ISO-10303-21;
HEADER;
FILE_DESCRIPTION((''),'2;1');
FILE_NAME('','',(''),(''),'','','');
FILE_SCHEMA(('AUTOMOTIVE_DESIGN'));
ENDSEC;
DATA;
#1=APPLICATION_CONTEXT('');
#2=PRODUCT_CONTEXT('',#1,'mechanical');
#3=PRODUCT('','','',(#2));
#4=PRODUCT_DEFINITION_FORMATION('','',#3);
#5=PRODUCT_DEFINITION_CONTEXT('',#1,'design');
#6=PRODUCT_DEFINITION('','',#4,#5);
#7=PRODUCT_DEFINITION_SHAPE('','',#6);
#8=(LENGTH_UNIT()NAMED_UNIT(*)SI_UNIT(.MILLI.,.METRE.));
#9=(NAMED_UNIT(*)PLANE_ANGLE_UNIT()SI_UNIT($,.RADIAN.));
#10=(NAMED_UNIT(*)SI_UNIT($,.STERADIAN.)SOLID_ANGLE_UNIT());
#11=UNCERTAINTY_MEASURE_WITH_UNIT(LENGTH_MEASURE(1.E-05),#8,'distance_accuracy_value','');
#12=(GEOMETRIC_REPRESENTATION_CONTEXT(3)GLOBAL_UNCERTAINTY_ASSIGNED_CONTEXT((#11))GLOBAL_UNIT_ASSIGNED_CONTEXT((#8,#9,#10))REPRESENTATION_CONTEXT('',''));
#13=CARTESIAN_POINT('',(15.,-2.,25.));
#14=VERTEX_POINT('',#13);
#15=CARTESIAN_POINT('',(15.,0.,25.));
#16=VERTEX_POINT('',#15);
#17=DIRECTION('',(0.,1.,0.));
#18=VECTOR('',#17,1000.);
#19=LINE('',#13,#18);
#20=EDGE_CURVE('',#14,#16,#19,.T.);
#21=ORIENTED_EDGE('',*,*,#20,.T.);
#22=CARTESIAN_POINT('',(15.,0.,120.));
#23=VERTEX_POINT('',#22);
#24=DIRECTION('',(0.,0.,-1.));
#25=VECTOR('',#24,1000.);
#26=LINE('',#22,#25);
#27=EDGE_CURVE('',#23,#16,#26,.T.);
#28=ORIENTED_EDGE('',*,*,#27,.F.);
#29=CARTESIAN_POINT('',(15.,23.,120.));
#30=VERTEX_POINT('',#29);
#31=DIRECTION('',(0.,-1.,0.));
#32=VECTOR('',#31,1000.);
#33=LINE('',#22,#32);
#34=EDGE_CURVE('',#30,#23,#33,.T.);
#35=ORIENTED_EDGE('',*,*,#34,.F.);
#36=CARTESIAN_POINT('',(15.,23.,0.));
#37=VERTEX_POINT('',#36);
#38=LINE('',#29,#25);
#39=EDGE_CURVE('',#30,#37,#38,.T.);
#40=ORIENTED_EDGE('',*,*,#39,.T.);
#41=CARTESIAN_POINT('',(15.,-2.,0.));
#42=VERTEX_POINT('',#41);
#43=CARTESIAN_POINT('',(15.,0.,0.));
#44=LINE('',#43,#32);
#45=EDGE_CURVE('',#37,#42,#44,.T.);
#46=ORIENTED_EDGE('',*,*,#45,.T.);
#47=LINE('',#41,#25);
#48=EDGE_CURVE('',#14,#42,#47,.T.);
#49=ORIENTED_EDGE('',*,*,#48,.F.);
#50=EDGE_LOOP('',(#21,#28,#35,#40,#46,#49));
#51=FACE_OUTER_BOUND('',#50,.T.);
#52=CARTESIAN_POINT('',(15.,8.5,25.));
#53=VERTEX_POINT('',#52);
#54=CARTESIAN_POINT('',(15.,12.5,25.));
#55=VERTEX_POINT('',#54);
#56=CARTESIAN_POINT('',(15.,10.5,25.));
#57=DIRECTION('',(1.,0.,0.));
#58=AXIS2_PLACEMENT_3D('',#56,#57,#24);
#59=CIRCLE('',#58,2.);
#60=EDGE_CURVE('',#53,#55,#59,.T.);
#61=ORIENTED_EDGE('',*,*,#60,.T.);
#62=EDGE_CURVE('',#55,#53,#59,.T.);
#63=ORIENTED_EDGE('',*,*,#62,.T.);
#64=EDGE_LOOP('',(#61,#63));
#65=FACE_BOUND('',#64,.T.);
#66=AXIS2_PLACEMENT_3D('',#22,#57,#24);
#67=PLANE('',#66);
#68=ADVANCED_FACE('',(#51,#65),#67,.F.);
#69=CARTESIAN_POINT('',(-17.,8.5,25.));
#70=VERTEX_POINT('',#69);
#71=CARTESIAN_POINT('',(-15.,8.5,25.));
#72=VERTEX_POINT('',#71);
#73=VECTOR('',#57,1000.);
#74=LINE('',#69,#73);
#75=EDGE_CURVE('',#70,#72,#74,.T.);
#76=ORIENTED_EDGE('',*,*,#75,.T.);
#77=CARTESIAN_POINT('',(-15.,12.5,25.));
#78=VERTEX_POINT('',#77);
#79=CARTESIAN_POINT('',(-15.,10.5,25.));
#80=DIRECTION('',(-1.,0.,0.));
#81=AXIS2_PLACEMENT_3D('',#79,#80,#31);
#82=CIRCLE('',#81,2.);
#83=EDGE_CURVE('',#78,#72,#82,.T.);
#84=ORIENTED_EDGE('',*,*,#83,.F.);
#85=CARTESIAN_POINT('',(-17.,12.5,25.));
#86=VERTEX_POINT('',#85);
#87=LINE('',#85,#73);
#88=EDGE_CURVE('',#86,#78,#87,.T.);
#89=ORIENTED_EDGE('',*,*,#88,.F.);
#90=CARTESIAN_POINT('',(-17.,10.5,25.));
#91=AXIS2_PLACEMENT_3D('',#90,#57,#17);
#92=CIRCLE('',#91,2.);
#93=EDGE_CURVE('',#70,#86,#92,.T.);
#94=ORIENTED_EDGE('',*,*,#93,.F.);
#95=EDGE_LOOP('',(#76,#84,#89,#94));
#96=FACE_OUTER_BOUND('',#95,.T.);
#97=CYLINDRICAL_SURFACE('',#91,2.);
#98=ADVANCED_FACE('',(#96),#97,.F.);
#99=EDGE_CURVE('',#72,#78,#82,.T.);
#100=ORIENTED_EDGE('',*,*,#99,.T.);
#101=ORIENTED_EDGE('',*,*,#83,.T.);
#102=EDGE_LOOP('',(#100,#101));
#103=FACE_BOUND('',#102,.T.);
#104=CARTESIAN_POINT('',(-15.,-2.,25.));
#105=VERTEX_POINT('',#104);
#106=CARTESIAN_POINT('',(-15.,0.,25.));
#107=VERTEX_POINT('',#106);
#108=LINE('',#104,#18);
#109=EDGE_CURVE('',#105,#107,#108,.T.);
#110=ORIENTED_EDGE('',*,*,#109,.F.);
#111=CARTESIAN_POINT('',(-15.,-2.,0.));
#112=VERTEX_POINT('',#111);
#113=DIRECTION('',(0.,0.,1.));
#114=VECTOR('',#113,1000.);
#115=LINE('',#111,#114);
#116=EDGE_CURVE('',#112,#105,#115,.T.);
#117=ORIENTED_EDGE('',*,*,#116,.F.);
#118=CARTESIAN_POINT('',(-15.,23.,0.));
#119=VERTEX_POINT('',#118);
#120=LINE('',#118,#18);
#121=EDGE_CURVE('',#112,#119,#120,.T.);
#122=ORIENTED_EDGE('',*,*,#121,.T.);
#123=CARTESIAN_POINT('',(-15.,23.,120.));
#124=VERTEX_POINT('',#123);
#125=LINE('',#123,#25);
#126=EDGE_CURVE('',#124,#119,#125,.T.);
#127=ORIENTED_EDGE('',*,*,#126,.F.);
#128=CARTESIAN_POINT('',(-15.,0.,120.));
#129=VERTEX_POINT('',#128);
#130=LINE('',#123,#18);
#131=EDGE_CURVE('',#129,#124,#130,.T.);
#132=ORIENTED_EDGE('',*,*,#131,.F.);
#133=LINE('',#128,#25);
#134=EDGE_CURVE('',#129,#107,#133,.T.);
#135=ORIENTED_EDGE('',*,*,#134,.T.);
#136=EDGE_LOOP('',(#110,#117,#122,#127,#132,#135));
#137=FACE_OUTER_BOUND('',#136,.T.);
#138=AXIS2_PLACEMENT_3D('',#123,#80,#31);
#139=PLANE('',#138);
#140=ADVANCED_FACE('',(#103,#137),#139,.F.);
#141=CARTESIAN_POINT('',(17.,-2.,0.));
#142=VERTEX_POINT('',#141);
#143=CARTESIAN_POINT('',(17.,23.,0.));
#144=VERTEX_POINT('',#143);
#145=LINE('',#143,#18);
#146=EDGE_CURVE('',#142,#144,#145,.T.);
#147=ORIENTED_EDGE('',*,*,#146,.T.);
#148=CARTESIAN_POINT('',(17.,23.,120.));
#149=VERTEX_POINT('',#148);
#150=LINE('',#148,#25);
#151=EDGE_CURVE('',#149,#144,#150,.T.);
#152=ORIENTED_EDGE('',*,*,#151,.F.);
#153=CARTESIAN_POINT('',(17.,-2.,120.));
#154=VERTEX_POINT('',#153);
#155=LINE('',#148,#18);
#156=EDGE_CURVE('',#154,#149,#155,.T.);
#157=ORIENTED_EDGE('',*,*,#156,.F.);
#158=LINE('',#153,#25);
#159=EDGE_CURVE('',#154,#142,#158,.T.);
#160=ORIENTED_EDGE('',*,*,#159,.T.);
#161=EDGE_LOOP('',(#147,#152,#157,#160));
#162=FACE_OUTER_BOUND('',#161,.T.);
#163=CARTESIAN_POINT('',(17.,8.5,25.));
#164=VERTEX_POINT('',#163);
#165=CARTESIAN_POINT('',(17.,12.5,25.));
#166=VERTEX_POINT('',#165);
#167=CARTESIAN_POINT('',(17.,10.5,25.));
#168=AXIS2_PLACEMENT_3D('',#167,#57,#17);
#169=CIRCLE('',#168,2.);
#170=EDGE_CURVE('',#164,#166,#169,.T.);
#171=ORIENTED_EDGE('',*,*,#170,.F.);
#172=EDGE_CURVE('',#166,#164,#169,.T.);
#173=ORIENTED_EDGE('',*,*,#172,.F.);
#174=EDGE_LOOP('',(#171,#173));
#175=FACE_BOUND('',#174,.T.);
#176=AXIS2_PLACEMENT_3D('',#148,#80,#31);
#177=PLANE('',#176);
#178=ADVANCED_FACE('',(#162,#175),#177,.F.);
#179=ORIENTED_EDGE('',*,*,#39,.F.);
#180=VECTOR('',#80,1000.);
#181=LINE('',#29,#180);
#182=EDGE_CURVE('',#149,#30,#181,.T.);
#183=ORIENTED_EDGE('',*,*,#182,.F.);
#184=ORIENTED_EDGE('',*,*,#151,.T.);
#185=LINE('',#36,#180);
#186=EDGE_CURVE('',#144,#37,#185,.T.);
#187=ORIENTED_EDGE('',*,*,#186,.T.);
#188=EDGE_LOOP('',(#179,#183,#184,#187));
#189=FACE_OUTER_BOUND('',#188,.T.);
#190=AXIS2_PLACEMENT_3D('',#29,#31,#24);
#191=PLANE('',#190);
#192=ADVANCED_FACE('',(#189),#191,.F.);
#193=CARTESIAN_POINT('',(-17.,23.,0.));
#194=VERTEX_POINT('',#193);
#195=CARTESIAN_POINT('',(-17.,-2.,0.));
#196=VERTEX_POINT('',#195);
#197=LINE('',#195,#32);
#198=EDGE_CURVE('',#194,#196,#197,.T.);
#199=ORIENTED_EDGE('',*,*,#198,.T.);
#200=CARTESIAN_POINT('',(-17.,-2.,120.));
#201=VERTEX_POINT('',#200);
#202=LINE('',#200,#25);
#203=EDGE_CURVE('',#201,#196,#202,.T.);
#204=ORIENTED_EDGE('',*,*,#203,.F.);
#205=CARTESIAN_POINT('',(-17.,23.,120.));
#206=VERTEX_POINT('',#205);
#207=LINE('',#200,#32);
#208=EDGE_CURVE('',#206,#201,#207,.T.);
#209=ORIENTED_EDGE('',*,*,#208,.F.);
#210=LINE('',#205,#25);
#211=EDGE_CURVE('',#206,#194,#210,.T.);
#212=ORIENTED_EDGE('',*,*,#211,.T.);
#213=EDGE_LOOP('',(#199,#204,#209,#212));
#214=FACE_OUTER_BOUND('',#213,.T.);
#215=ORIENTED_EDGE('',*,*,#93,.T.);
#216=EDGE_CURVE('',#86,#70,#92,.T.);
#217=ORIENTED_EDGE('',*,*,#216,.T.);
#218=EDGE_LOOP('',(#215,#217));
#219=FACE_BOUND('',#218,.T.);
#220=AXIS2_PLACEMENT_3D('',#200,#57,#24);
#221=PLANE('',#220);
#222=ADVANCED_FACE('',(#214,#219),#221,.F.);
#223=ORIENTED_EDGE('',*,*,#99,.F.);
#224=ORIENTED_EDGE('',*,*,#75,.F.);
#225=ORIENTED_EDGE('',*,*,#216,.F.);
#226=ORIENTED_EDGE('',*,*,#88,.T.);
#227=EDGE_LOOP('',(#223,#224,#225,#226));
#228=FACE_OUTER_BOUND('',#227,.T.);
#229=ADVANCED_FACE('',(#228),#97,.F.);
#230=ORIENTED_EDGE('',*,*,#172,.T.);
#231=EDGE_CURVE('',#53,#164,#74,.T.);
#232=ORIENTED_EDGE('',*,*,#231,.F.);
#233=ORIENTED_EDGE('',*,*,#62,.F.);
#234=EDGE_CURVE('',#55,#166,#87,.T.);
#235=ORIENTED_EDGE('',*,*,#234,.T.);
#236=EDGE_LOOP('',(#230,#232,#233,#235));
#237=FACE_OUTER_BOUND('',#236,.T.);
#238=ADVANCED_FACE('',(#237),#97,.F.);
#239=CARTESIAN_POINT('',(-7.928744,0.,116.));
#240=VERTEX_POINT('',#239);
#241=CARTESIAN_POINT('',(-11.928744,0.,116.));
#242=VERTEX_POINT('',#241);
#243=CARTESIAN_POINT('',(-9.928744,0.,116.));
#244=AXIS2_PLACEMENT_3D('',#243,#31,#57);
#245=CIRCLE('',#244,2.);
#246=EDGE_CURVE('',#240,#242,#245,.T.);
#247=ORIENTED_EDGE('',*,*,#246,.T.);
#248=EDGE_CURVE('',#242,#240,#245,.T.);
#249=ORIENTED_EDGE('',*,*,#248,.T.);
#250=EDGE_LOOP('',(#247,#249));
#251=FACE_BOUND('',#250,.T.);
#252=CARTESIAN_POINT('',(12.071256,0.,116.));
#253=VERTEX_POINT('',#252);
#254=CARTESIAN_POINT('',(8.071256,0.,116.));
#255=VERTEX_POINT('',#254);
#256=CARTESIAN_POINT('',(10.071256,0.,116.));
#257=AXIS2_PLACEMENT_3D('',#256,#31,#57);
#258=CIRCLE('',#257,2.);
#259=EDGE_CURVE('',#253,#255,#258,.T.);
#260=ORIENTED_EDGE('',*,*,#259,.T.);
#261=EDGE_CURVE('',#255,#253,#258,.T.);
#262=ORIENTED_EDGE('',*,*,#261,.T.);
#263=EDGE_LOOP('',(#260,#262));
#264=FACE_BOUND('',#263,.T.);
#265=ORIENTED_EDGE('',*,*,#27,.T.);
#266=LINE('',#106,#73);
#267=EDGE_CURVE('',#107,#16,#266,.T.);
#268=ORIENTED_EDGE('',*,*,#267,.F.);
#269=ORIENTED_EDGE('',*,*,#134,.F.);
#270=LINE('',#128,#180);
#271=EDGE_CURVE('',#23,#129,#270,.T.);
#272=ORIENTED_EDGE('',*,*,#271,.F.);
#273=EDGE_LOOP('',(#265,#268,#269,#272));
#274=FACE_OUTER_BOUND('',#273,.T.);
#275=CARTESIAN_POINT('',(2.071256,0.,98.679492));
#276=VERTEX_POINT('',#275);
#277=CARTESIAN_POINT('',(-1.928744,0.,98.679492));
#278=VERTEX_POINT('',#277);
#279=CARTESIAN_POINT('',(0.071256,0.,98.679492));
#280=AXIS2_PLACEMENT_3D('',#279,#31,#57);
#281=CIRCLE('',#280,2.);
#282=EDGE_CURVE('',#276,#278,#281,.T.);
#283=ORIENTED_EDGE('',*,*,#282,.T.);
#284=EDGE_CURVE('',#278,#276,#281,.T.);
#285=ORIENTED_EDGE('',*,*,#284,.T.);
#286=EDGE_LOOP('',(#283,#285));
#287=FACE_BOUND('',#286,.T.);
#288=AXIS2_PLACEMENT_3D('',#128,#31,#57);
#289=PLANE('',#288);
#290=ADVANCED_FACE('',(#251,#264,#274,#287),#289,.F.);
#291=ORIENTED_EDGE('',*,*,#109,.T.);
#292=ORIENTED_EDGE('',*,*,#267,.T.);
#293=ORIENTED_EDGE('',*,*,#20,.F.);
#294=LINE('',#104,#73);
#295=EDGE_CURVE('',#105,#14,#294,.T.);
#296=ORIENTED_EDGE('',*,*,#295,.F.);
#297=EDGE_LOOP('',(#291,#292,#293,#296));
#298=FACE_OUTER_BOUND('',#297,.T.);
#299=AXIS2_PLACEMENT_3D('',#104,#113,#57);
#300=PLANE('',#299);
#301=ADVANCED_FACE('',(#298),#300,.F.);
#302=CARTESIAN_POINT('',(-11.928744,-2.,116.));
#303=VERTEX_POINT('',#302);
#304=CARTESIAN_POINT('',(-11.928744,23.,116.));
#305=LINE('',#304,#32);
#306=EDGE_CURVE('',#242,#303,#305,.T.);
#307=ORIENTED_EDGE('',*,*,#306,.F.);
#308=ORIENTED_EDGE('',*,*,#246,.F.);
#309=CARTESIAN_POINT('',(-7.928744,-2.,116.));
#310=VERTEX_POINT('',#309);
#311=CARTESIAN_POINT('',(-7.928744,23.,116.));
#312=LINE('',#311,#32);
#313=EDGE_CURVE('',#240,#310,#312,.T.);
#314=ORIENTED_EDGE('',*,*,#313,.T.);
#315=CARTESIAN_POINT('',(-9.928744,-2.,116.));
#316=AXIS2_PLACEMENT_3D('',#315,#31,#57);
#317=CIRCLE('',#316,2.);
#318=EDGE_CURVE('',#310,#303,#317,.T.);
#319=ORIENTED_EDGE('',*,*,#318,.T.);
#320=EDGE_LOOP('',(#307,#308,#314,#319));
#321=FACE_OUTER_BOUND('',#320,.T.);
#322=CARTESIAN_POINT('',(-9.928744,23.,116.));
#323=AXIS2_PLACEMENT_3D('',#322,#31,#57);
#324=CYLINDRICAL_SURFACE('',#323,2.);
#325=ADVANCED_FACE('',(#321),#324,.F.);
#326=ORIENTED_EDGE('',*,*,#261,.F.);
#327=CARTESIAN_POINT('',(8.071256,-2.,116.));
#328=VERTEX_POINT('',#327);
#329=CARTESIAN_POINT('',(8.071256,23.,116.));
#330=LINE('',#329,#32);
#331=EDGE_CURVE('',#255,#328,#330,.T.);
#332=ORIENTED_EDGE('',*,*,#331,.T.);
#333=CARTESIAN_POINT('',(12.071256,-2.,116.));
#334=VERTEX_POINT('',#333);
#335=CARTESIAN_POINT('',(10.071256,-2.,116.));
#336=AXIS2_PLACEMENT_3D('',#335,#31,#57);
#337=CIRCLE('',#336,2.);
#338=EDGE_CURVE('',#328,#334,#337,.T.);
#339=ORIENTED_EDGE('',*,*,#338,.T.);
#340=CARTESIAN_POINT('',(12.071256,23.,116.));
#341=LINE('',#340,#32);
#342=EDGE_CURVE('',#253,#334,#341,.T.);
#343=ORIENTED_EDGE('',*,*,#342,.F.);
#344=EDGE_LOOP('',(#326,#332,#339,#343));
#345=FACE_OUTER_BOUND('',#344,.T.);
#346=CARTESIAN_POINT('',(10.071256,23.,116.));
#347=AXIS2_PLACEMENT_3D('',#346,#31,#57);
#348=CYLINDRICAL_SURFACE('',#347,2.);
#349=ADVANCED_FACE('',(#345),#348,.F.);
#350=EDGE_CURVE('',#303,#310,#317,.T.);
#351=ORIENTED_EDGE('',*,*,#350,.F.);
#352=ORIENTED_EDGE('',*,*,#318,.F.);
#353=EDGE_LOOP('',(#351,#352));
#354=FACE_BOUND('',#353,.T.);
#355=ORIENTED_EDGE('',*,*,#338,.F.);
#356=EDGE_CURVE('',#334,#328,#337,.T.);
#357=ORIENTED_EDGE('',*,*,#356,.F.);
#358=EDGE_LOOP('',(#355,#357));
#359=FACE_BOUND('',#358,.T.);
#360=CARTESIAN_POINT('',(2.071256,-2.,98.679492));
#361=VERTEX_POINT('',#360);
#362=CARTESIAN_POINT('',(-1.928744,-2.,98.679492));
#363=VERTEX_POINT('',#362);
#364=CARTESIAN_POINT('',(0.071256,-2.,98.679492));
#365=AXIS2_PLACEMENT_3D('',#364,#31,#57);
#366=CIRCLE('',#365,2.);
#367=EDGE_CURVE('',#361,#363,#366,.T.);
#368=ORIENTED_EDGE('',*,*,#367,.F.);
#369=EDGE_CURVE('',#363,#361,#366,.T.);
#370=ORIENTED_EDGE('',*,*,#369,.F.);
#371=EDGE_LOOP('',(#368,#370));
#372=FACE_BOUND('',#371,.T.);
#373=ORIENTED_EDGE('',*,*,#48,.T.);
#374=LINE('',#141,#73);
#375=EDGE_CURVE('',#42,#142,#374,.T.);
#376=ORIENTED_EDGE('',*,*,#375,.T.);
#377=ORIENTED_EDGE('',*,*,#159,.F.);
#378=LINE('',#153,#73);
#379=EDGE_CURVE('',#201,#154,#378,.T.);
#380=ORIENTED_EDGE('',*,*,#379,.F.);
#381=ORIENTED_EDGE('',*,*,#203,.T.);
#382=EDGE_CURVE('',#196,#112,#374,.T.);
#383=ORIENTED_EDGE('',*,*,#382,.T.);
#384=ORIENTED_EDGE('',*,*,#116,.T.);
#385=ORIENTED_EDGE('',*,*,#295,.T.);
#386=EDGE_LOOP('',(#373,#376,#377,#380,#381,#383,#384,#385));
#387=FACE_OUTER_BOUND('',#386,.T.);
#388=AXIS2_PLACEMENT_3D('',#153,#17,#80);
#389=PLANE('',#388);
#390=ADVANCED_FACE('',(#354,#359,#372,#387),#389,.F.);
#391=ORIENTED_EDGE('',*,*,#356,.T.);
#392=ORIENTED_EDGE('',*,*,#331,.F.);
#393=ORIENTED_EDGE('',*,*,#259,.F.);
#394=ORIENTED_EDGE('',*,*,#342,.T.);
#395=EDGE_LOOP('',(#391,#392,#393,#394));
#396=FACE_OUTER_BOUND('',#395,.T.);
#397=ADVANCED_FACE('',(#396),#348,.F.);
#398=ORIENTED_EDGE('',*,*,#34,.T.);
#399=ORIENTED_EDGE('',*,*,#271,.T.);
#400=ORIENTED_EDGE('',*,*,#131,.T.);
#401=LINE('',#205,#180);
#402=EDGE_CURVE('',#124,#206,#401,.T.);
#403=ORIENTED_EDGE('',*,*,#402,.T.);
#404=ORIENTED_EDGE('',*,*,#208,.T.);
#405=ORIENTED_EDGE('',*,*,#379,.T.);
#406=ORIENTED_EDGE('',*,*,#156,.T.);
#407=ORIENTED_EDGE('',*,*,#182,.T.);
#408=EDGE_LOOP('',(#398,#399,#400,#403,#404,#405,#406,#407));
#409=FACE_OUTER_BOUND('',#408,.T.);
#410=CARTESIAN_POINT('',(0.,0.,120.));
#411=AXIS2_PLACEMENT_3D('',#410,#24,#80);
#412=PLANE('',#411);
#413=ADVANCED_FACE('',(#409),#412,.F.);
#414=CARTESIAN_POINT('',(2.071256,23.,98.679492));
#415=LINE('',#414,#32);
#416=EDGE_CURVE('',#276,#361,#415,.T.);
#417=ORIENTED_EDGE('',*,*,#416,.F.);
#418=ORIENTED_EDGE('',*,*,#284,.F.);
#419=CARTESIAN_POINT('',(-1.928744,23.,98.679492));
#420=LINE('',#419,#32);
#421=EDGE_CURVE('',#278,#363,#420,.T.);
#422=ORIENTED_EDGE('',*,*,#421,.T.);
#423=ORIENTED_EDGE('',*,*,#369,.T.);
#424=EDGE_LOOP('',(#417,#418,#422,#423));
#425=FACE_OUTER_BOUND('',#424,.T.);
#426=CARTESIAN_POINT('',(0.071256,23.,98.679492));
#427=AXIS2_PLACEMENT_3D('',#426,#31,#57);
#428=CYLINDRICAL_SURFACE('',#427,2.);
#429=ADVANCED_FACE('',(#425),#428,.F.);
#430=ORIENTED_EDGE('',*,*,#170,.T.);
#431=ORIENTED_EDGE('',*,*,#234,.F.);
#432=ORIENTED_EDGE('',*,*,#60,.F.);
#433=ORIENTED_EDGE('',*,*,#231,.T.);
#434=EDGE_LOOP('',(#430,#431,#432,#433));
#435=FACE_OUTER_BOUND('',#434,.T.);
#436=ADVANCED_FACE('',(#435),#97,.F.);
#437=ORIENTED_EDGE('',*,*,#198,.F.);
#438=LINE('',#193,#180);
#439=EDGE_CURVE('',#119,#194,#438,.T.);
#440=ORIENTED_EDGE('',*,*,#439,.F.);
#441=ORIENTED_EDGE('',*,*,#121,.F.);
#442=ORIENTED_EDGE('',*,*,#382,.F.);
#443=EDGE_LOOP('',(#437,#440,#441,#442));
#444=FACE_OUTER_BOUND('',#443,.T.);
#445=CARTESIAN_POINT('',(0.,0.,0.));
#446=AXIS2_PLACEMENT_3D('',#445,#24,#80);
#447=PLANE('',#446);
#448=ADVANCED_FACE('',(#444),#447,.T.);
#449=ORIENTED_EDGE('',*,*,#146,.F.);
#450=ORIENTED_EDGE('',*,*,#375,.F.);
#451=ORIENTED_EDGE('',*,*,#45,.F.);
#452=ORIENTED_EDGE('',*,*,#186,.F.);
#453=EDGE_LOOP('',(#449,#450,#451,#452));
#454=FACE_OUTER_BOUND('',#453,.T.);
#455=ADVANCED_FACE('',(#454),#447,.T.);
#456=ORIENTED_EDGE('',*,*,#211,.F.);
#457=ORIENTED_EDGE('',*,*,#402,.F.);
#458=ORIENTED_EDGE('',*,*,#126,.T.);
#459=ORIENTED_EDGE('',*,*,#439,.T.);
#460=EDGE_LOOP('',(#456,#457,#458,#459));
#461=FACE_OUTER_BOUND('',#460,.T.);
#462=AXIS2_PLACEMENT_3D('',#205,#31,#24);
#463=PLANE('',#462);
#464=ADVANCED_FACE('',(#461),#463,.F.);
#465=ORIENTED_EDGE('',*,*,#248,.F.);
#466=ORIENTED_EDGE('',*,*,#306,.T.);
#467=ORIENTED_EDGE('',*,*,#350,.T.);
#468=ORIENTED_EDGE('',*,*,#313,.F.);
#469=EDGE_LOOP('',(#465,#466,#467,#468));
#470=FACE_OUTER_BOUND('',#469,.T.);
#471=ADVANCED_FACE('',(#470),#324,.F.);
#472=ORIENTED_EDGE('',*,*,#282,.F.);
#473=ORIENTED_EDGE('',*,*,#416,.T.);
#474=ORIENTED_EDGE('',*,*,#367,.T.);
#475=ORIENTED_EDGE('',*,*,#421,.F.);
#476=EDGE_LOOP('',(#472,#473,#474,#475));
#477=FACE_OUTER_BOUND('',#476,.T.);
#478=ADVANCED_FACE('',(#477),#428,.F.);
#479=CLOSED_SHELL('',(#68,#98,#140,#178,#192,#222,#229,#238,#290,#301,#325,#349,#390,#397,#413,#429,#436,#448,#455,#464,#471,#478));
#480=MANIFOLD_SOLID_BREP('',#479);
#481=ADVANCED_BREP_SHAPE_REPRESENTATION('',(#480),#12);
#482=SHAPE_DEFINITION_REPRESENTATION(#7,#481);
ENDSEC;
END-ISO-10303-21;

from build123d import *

# Parameters (mm, degrees)
BOSS_EXTRUDE1_DEPTH = 120
SKETCH2_R           = 2
CUT_EXTRUDE1_DEPTH  = 124.749747474
SKETCH3_W           = 30
SKETCH3_H           = 25
CUT_EXTRUDE2_DEPTH  = 124.3612581
SKETCH4_R           = 2
CUT_EXTRUDE3_DEPTH  = 127.82665335


with BuildPart() as part:
    # Sketch1 → Boss-Extrude1 (new body)
    with BuildSketch(Plane.XY):
        Polygon((-15, 23), (-15, 0), (15, 0), (15, 23), (17, 23), (17, -2), (-17, -2), (-17, 23), align=None)
    extrude(amount=BOSS_EXTRUDE1_DEPTH)

    # Sketch2 → Cut-Extrude1 (cut, through all)
    with BuildSketch(Plane.XZ.offset(2)):
        with Locations((0.071255778, 98.679491924)):
            Circle(SKETCH2_R)
        with Locations((10.071255778, 116)):
            Circle(SKETCH2_R)
        with Locations((-9.928744222, 116)):
            Circle(SKETCH2_R)
    extrude(amount=-CUT_EXTRUDE1_DEPTH, mode=Mode.SUBTRACT)

    # Sketch3 → Cut-Extrude2 (cut, through all)
    with BuildSketch(Plane(origin=(0, 0, 0), x_dir=(1, 0, 0), z_dir=(0, 1, 0))):
        with Locations((0, -12.5)):
            Rectangle(SKETCH3_W, SKETCH3_H)
    extrude(amount=-CUT_EXTRUDE2_DEPTH, mode=Mode.SUBTRACT)

    # Sketch4 → Cut-Extrude3 (cut, through all)
    with BuildSketch(Plane(origin=(17, 0, 0), x_dir=(0, 0, -1), z_dir=(1, 0, 0))):
        with Locations(Location((-25, 10.5, 0), (0, 0, 90))):
            Circle(SKETCH4_R)
    extrude(amount=-CUT_EXTRUDE3_DEPTH, mode=Mode.SUBTRACT)


solid = part.part
